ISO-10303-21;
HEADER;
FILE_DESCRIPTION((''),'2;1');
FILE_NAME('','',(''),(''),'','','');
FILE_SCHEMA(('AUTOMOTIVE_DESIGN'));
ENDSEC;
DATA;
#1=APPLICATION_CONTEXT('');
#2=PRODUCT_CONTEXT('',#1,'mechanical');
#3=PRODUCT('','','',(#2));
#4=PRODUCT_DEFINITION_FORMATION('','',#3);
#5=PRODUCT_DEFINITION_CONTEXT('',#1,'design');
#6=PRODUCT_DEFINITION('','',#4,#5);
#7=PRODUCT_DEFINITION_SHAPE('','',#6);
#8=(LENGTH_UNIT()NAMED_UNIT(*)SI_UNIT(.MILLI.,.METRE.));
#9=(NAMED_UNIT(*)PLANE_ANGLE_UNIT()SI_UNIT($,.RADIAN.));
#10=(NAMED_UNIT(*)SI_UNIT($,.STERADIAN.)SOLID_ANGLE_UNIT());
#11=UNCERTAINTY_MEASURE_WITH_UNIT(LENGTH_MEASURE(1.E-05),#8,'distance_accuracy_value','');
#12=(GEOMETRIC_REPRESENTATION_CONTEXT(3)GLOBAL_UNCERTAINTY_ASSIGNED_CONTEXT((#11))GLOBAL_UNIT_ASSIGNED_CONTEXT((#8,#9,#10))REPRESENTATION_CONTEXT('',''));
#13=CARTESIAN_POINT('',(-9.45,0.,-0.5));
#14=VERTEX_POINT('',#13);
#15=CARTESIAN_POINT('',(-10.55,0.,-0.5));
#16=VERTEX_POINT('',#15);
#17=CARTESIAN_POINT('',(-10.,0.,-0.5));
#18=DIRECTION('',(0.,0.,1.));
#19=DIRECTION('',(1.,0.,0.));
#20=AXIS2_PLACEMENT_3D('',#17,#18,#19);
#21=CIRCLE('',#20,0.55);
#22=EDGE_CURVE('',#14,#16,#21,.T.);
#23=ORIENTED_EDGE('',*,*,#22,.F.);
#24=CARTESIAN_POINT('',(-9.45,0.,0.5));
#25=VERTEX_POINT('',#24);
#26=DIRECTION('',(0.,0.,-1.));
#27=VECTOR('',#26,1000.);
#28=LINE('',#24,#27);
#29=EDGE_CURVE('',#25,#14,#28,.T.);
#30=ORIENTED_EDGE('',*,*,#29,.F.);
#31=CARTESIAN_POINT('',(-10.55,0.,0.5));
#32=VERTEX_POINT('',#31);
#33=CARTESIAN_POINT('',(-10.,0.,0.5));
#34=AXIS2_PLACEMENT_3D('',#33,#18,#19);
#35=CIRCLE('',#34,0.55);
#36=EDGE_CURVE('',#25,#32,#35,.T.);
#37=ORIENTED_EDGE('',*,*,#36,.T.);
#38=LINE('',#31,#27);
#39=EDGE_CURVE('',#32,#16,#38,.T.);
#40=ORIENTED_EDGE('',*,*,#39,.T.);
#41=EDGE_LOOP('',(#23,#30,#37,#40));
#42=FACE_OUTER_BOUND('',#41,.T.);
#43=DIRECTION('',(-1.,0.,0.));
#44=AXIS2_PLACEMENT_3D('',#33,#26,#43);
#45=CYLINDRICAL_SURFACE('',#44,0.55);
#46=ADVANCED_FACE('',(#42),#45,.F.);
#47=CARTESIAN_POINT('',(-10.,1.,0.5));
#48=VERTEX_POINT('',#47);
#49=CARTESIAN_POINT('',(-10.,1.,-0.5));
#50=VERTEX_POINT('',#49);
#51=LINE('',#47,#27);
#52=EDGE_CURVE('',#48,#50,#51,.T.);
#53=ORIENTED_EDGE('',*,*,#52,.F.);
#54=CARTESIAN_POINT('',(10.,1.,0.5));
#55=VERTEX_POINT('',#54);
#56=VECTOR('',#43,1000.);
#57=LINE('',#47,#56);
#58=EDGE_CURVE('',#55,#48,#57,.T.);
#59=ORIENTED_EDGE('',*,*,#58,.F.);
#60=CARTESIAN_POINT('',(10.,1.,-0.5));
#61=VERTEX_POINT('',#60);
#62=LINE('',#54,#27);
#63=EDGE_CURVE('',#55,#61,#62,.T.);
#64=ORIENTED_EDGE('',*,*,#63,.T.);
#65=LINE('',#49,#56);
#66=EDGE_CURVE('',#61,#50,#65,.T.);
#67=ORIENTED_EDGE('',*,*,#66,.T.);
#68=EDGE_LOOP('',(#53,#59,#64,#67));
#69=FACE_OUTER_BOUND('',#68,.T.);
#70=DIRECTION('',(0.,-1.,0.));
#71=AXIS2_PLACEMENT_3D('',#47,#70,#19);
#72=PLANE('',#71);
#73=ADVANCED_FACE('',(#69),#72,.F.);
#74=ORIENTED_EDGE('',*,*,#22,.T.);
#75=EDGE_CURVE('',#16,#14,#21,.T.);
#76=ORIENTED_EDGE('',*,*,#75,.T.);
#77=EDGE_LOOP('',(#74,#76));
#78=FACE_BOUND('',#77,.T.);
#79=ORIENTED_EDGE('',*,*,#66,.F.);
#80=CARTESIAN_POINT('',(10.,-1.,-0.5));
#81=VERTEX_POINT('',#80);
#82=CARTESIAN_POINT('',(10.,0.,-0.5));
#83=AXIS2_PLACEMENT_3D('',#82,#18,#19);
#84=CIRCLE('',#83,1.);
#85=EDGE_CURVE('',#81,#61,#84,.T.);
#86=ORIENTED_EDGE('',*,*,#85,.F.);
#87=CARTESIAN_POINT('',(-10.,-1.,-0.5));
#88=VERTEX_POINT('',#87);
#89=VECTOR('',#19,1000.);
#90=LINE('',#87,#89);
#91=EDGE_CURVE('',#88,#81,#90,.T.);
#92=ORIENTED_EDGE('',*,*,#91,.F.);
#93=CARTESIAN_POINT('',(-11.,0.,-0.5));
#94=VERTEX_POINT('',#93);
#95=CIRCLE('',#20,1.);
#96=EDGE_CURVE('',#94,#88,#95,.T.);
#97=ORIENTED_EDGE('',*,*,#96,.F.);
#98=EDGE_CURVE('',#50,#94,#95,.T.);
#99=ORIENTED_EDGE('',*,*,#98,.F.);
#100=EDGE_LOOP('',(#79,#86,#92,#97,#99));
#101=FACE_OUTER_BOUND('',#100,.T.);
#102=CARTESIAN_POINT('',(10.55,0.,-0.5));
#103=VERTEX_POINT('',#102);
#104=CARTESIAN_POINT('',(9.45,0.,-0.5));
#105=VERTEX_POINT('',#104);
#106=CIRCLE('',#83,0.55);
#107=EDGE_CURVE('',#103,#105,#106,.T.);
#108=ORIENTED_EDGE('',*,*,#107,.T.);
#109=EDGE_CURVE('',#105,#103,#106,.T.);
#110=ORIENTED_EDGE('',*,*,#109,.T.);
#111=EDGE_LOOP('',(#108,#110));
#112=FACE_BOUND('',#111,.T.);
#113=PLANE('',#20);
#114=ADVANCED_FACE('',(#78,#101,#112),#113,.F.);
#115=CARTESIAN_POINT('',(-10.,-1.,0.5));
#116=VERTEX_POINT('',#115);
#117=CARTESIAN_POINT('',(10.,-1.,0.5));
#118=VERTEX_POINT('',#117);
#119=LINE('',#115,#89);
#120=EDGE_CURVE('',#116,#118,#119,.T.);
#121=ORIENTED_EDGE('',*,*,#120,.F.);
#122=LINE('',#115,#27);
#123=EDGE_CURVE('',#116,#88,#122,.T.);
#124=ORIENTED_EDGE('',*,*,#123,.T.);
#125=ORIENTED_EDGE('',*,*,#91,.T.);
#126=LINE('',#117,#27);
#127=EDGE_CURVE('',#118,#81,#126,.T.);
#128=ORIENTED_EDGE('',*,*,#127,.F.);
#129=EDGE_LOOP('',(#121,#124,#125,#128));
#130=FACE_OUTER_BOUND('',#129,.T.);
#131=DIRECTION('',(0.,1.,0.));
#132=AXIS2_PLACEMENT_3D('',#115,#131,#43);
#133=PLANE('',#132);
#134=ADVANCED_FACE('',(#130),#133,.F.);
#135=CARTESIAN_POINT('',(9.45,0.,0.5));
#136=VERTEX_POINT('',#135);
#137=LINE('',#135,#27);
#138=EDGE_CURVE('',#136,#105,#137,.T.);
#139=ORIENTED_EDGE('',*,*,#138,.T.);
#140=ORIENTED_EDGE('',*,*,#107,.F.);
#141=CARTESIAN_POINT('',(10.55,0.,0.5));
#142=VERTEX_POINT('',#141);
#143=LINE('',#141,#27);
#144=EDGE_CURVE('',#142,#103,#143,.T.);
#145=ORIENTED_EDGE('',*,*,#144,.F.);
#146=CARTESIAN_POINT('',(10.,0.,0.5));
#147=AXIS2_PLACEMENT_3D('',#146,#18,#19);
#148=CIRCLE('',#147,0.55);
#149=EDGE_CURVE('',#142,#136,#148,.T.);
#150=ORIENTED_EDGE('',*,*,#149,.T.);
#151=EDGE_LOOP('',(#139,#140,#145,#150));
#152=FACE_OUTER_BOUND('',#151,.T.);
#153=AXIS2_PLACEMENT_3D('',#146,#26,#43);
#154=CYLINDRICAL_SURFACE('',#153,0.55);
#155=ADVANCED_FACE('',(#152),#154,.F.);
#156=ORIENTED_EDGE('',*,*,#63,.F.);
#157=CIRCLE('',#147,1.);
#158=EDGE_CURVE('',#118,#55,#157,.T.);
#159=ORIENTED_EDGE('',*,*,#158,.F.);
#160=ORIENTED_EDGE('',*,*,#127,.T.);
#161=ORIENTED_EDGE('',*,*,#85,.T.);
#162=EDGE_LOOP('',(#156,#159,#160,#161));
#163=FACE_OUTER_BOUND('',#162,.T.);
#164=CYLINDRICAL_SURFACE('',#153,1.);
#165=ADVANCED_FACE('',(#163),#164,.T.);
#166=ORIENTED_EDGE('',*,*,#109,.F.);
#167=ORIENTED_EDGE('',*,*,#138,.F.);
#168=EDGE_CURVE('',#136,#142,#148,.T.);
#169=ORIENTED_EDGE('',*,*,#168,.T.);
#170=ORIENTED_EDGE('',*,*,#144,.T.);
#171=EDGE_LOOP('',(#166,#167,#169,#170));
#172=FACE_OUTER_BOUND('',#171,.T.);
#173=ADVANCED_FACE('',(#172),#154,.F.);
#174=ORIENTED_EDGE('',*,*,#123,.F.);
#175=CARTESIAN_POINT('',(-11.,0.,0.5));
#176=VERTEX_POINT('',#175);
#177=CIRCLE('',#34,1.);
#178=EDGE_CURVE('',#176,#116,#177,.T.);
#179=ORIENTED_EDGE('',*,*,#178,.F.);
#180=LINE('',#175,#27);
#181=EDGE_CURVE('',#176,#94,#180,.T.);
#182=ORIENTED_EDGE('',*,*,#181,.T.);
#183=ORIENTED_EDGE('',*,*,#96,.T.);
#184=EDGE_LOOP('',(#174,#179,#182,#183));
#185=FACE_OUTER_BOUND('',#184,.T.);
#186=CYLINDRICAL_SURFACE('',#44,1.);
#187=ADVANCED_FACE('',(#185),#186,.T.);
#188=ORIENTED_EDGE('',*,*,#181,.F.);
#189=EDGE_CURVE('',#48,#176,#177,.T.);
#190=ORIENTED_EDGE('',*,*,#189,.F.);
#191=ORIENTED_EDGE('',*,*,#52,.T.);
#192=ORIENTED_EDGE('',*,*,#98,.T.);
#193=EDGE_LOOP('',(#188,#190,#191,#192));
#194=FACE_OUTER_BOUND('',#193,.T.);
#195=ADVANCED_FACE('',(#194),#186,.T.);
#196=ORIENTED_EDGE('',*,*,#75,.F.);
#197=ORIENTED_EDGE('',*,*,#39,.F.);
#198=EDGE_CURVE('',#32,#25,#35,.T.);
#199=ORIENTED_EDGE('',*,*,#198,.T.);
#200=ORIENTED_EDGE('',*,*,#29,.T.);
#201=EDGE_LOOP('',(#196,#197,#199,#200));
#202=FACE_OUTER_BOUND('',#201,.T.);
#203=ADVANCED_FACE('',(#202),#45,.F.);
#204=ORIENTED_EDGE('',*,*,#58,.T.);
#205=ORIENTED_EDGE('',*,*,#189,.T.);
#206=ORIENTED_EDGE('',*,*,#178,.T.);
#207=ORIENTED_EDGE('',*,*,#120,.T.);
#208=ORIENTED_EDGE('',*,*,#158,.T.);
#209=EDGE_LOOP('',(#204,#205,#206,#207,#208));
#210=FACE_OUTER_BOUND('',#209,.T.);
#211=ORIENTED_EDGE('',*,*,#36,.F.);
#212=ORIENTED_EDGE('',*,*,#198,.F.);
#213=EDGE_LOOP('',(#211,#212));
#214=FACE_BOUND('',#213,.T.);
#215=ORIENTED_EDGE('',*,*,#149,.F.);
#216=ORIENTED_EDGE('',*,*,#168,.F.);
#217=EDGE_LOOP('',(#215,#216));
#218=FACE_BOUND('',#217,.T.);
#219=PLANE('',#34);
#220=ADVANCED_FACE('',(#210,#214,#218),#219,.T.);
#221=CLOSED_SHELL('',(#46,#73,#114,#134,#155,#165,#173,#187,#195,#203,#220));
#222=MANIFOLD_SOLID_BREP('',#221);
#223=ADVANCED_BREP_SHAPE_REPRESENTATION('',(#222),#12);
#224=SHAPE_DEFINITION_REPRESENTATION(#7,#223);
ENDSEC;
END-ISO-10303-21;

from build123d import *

# Parameters (mm, degrees)
SKETCH1_R           = 0.55
THIGH1_LENGTH_DEPTH = 0.5


with BuildPart() as part:
    # Sketch1 → Thigh1 length (new, symmetric)
    with BuildSketch(Plane.XY):
        with BuildLine():
            Line((-10, 1), (10, 1))
            ThreePointArc((10, 1), (11, 0), (10, -1))
            Line((10, -1), (-10, -1))
            ThreePointArc((-10, -1), (-11, 0), (-10, 1))
        make_face()
        with Locations((-10, 0)):
            Circle(SKETCH1_R, mode=Mode.SUBTRACT)
        with Locations((10, 0)):
            Circle(SKETCH1_R, mode=Mode.SUBTRACT)
    extrude(amount=THIGH1_LENGTH_DEPTH, both=True)


solid = part.part
